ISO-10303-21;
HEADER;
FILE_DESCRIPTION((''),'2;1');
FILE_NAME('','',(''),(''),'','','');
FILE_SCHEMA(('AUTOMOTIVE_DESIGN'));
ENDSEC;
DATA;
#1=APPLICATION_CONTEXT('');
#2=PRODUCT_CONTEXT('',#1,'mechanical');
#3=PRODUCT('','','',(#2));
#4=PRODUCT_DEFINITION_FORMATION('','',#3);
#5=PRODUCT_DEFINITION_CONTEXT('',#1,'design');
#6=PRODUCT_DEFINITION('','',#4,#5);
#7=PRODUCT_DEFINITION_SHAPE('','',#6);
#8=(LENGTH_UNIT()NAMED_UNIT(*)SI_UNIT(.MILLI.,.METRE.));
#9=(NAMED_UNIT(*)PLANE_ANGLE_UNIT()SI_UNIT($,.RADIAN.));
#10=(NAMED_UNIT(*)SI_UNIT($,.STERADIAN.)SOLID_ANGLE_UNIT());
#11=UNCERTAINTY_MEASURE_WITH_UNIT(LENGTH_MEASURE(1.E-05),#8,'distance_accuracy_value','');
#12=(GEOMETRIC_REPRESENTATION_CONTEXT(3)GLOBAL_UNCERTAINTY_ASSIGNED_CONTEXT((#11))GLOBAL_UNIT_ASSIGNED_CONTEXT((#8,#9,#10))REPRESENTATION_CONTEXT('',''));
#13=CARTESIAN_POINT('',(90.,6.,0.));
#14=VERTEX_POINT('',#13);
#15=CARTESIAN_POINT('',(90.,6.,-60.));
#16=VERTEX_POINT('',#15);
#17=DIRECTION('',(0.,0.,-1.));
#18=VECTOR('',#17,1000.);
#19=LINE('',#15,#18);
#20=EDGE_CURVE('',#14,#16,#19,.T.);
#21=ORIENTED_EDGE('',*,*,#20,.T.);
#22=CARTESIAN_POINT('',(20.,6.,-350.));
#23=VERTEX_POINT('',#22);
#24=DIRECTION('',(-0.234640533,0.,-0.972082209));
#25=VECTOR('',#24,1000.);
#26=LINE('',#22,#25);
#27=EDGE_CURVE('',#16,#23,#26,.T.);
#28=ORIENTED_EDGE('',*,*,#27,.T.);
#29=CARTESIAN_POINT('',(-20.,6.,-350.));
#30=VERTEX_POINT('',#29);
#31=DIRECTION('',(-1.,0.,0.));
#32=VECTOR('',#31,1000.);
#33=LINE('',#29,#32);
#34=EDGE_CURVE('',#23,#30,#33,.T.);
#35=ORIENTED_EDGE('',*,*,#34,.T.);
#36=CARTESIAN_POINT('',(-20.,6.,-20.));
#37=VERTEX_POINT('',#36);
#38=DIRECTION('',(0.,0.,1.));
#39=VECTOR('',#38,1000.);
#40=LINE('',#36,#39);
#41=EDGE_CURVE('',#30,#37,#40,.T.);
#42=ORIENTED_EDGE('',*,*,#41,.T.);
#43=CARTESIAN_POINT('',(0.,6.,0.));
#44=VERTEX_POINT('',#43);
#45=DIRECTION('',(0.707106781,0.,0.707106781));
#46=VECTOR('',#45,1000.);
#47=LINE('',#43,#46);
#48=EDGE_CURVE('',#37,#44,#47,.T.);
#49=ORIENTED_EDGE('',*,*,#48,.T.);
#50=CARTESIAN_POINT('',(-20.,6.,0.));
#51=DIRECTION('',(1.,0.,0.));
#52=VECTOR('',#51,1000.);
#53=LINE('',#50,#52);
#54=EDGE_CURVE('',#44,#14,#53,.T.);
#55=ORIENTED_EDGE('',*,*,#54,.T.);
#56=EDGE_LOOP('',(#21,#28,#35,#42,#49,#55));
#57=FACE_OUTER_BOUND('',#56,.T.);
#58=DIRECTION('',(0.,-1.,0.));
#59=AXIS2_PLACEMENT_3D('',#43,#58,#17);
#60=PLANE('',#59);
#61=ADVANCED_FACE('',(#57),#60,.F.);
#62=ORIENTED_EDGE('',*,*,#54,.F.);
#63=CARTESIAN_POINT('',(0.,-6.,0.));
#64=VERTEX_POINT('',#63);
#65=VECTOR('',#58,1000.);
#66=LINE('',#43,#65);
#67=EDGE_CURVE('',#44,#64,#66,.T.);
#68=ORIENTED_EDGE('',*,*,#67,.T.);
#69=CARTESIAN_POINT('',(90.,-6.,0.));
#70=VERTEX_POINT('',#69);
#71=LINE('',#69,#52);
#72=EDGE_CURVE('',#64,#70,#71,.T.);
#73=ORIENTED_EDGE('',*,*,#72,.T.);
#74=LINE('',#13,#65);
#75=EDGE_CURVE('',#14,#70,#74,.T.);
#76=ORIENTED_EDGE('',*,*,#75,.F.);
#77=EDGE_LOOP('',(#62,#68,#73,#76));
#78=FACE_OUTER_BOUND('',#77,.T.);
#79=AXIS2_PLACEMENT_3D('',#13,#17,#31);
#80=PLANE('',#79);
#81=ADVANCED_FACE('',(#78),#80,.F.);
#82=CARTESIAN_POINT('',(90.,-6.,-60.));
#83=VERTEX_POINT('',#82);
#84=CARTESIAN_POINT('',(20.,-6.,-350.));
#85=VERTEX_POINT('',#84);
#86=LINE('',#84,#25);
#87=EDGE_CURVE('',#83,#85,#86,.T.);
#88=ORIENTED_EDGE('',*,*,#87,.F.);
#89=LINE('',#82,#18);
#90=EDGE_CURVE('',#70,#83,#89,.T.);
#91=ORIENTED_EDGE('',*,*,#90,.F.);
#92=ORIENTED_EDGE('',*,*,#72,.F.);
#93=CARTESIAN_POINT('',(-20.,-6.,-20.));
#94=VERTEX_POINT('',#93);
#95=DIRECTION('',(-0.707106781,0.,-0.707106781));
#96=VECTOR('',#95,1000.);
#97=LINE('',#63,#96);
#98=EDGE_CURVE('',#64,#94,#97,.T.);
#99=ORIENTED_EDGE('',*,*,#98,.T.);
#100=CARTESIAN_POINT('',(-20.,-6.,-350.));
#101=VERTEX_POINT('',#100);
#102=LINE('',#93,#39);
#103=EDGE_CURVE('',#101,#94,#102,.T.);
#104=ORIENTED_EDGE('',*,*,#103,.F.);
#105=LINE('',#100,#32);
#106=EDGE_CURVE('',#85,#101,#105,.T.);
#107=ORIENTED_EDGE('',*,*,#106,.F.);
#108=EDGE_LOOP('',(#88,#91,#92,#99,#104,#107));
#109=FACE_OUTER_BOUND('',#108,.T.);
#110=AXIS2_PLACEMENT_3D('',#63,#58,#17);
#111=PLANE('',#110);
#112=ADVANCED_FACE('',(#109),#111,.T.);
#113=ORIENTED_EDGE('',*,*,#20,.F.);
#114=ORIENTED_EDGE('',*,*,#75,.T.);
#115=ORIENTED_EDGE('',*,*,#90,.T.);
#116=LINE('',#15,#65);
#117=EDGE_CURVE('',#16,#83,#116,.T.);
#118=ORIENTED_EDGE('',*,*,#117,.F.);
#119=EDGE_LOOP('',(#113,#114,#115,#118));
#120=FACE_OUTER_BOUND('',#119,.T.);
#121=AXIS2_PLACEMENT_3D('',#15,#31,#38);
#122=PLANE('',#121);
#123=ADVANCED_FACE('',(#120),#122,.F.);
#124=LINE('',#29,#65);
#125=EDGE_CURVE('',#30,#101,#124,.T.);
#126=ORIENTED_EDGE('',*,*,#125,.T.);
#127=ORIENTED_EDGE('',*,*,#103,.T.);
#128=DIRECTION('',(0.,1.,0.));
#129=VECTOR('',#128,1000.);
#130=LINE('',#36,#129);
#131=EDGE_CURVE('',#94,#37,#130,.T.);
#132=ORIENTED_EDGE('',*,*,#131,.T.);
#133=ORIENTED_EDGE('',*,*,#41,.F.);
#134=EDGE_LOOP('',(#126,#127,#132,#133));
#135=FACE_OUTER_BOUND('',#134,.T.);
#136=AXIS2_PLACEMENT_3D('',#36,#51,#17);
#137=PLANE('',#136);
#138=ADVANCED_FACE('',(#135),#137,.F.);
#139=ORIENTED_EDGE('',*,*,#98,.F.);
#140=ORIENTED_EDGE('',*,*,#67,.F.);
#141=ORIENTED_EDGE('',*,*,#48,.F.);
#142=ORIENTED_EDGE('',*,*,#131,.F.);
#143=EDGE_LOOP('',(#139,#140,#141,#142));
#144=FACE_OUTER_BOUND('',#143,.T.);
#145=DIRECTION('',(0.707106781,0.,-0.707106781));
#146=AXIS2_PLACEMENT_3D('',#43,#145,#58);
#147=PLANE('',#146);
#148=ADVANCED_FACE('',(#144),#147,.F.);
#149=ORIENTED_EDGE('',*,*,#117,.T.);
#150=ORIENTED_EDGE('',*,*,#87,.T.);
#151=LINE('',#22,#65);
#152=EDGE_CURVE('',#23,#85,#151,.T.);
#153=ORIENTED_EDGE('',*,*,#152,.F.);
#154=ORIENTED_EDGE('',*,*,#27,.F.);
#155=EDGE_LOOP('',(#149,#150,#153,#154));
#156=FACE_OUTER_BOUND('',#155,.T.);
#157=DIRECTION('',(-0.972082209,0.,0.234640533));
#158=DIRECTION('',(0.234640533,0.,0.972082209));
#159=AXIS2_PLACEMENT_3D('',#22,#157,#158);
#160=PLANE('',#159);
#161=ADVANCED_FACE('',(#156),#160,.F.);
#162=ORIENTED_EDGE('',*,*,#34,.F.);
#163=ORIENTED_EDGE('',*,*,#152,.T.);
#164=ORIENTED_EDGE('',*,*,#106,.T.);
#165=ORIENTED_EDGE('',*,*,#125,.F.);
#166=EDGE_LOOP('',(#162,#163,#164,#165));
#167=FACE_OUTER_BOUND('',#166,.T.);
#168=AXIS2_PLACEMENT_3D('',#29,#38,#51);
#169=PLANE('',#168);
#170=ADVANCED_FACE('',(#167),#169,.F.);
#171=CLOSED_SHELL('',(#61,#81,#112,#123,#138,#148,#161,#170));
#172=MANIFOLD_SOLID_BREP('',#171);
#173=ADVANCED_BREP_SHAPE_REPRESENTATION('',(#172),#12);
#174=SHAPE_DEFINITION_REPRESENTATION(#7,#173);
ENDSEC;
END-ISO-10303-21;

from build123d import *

# Parameters (mm, degrees)
BOSS_EXTRUDE1_DEPTH = 6
CHAMFER1_SIZE       = 20


with BuildPart() as part:
    # Sketch1 → Boss-Extrude1 (new, symmetric)
    with BuildSketch(Plane(origin=(0, 0, 0), x_dir=(1, 0, 0), z_dir=(0, 1, 0))):
        Polygon((-20, 20), (-20, 350), (20, 350), (90, 60), (90, 0), (0, 0), (-20, 0), align=None)
    extrude(amount=BOSS_EXTRUDE1_DEPTH, both=True)

    # Chamfer1
    chamfer1_edges = [part.edges().sort_by_distance(p)[0] for p in [
        (-20, 0, 0),
    ]]
    chamfer(chamfer1_edges, length=CHAMFER1_SIZE)


solid = part.part
